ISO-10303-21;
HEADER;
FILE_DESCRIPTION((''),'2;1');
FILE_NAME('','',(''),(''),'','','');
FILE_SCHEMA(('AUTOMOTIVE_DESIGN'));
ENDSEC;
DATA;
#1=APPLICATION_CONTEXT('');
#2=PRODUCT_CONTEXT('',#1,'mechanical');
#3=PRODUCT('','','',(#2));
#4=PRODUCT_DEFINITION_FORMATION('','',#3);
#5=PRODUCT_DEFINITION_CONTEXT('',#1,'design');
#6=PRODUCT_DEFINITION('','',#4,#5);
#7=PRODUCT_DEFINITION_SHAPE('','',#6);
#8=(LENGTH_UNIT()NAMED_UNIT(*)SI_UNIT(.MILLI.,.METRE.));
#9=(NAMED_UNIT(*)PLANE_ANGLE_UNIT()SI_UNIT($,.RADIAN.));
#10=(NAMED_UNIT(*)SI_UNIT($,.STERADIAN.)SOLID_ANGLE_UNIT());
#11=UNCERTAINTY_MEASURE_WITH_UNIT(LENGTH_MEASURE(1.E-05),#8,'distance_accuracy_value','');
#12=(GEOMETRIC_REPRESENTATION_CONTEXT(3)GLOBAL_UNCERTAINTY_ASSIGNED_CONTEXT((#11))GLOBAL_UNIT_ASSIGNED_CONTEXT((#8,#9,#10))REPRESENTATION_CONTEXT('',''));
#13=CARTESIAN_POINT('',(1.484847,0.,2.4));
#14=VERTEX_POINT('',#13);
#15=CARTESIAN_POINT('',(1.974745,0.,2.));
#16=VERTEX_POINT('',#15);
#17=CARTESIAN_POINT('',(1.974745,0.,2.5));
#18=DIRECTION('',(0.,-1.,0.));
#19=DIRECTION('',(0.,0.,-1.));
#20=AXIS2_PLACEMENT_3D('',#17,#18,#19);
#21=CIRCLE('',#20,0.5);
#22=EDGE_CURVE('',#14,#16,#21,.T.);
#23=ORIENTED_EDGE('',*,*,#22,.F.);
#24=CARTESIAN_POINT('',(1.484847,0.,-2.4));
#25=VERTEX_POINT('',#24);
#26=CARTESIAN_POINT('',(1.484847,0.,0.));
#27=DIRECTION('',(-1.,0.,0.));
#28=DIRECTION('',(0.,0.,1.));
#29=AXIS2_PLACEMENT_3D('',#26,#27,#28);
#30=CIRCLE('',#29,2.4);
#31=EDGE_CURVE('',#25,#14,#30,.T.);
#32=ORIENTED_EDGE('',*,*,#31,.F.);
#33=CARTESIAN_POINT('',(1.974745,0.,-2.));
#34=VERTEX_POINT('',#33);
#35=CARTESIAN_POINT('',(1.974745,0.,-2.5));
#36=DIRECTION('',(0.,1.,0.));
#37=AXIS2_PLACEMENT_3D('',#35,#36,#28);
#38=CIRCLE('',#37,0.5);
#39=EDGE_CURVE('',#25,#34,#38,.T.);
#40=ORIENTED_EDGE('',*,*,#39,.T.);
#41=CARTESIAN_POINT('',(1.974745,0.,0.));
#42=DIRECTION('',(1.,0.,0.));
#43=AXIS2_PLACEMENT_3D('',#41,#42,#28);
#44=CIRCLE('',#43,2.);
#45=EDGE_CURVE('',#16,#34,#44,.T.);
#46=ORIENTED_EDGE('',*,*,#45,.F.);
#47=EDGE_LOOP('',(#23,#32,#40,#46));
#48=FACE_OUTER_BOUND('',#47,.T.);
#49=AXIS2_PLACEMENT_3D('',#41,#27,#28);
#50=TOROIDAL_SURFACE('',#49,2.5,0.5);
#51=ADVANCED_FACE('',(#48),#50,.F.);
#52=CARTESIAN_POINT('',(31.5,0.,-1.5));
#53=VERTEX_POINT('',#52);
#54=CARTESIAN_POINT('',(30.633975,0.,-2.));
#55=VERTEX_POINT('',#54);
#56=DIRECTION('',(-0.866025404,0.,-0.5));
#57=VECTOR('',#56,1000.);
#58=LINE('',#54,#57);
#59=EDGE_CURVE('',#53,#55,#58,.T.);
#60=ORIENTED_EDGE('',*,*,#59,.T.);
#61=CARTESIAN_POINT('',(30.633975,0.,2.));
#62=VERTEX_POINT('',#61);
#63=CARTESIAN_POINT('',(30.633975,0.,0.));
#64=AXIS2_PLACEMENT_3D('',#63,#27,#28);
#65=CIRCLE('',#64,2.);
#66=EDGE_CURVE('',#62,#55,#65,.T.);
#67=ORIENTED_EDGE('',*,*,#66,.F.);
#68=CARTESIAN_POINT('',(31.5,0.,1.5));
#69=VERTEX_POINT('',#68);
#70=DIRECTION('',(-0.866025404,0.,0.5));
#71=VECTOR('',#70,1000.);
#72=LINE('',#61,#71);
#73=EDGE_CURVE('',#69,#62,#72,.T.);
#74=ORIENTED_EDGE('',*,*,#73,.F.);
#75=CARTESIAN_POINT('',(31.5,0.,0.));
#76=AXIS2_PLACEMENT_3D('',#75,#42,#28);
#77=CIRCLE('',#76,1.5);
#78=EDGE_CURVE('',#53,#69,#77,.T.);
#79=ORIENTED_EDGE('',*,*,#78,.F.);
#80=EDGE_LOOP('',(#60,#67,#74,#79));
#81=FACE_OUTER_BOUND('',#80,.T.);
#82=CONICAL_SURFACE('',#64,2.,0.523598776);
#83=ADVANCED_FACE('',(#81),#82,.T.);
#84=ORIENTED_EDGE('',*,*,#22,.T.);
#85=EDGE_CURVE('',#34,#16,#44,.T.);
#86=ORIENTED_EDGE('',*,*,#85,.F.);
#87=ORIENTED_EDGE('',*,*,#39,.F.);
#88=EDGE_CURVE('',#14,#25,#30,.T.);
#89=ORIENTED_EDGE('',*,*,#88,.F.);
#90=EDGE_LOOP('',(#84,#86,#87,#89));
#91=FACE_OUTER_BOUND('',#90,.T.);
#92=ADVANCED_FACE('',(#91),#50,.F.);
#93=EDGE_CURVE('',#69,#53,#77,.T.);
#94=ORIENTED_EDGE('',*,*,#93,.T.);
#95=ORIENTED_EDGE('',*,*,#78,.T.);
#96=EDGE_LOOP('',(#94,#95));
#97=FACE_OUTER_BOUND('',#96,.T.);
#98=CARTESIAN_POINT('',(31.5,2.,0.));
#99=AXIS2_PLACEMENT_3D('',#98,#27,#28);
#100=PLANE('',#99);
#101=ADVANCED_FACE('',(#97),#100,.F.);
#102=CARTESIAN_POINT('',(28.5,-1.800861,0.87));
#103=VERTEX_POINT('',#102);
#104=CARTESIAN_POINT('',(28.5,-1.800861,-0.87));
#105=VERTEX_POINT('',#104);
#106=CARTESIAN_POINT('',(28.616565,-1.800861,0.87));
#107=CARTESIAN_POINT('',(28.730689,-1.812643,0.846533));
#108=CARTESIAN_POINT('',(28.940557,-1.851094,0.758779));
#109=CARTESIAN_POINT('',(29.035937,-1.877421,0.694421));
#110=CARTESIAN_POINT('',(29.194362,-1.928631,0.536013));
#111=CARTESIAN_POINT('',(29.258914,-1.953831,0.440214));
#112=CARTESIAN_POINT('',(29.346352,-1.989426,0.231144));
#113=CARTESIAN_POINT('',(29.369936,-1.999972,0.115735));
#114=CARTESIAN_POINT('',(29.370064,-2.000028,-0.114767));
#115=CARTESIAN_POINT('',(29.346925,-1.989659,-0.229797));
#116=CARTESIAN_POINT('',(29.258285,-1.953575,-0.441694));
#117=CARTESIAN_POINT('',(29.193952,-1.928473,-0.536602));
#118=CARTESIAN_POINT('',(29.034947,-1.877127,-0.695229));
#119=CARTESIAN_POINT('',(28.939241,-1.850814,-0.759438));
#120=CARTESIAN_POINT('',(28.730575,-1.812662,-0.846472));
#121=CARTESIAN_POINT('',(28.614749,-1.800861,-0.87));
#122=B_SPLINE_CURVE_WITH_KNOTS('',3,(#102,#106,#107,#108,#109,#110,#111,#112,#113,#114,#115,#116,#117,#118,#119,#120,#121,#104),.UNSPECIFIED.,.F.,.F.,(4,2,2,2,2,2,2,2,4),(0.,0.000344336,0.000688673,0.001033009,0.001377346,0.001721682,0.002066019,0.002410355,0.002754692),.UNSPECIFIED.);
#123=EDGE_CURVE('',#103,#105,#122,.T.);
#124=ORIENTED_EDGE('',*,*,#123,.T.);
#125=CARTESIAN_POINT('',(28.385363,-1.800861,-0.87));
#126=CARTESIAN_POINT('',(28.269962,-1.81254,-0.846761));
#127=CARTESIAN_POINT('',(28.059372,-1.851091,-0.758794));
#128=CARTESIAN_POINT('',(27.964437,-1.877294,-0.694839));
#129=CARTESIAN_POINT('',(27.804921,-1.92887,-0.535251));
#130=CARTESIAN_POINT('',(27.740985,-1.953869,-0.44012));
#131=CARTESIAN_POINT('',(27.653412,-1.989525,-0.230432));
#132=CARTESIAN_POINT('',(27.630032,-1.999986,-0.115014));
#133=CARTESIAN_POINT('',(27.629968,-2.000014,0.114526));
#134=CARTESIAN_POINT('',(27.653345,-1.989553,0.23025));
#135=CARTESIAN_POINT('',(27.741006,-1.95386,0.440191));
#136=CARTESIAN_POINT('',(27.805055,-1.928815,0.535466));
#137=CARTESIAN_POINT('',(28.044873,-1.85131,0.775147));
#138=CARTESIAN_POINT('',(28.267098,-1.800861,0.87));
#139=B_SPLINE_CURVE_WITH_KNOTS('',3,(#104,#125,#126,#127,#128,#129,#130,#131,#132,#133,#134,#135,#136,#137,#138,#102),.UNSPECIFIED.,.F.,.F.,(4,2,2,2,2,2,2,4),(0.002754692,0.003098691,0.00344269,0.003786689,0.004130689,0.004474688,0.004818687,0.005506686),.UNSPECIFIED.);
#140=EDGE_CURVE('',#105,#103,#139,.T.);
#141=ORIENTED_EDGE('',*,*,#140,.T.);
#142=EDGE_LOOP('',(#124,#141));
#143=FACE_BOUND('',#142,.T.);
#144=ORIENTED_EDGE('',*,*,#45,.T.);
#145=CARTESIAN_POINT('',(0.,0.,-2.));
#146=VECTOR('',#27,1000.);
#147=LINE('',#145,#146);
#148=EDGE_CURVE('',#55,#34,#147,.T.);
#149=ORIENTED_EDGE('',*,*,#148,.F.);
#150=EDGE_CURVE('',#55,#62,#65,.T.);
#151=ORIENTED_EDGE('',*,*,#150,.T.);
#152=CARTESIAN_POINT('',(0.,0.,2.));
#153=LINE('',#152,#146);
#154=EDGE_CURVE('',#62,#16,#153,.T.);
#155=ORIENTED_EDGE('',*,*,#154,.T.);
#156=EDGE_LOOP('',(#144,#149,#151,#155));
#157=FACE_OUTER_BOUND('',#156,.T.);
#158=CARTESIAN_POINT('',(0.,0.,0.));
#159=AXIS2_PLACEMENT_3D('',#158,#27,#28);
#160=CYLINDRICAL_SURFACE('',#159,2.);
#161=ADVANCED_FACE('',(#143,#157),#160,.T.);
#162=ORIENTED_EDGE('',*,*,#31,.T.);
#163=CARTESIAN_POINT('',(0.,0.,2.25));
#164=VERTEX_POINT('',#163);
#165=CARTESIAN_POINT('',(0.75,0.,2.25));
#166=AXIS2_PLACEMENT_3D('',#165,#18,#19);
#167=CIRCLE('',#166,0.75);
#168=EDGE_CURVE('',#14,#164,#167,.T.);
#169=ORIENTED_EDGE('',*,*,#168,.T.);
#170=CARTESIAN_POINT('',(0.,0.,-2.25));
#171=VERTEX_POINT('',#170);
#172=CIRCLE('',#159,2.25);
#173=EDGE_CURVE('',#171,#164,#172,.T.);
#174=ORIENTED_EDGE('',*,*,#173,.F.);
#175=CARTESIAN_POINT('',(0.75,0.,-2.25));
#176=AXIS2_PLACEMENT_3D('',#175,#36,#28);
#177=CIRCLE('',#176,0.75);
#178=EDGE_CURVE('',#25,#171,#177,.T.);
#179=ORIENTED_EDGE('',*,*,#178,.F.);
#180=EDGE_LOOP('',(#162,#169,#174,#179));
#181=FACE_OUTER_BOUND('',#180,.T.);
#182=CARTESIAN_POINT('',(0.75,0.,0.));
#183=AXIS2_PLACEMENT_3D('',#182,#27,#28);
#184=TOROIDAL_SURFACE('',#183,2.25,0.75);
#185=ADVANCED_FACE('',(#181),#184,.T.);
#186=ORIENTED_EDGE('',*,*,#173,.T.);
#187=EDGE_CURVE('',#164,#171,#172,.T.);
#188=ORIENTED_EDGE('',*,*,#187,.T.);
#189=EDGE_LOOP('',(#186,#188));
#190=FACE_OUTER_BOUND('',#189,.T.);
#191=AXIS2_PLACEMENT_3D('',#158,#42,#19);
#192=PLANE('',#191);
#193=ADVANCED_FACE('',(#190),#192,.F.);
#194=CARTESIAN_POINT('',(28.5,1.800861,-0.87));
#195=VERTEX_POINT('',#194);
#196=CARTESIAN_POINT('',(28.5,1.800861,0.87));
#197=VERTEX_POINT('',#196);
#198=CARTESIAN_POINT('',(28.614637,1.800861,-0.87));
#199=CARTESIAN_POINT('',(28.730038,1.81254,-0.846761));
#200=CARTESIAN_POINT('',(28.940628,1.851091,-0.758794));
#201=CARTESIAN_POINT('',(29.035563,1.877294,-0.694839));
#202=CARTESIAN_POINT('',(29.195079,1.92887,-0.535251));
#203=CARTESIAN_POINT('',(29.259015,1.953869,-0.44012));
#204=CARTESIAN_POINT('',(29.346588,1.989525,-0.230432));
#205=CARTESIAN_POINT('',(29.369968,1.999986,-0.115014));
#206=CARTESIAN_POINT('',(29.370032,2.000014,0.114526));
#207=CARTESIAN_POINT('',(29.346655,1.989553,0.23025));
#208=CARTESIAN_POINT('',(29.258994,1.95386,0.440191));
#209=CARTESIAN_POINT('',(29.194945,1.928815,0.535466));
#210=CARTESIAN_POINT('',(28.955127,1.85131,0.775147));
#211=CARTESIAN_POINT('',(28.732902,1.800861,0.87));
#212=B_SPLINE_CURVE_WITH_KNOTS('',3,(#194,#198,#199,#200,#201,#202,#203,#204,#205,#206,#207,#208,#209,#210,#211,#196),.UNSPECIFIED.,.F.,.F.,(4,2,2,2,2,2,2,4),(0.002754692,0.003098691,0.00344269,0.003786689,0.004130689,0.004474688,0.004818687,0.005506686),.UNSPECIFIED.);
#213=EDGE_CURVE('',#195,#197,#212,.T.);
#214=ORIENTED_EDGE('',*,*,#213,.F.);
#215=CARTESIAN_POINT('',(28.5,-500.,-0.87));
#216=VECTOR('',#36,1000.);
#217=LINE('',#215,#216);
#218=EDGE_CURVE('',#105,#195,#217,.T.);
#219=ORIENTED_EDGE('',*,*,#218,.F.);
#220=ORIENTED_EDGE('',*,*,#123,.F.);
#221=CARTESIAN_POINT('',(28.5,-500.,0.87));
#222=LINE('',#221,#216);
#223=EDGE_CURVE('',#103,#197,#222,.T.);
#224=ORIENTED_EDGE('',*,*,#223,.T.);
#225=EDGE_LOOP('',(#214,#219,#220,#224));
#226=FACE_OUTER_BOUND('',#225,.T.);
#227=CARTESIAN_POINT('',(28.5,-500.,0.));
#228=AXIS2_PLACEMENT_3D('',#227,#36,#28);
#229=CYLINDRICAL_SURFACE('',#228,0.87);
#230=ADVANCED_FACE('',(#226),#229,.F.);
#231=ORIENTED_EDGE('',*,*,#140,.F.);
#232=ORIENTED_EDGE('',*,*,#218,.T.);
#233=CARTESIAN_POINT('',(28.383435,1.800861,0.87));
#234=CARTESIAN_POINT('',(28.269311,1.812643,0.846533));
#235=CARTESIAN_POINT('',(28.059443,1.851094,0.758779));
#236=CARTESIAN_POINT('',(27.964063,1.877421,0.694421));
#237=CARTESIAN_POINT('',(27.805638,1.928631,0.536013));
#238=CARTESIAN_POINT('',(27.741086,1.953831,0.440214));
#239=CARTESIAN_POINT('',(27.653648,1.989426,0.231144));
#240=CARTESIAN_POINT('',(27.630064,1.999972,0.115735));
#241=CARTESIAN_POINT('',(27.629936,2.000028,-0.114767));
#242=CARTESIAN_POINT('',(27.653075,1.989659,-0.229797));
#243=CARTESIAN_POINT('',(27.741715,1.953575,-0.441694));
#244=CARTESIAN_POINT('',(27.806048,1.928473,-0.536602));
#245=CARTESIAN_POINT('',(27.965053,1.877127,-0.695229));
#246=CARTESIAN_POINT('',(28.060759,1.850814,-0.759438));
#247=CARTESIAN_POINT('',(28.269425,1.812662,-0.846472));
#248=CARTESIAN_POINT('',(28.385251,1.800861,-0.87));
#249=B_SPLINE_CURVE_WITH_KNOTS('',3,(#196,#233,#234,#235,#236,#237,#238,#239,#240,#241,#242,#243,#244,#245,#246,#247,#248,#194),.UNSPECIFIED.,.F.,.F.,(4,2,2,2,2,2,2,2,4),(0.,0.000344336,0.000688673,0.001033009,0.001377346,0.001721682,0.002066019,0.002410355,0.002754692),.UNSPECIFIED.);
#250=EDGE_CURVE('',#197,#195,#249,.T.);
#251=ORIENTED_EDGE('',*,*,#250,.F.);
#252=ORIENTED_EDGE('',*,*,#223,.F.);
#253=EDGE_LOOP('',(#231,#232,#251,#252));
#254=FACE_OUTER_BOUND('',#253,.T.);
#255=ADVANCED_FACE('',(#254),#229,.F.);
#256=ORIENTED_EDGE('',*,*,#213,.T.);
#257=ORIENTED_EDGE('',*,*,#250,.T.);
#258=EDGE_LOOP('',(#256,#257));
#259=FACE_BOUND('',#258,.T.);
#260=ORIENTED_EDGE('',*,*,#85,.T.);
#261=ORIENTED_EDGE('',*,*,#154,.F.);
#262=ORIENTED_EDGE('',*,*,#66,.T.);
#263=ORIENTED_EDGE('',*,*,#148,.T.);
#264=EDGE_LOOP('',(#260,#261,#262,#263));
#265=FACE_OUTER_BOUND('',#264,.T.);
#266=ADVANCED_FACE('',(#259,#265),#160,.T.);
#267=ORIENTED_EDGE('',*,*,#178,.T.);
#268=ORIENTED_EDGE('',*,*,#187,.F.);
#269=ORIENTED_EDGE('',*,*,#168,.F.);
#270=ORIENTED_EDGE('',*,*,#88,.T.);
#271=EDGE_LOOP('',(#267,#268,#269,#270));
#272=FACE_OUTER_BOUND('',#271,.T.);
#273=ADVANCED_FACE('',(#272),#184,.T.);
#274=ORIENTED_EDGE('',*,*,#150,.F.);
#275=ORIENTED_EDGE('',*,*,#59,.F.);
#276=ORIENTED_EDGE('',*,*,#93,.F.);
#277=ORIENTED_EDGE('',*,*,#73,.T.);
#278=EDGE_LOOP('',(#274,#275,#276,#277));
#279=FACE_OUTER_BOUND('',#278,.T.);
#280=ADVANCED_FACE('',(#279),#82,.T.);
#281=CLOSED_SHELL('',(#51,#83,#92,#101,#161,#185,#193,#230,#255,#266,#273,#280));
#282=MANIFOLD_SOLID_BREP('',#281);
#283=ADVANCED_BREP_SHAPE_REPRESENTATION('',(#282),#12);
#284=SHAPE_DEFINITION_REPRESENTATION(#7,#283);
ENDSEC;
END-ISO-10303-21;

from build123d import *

# Parameters (mm, degrees)
FILLET_1_R          = 0.5
CHAMFER_1_SIZE      = 0.866025404
CHAMFER_1_SIZE2     = 0.5
SKETCH_2_R          = 0.87
CUT_EXTRUDE_1_DEPTH = 500


with BuildPart() as part:
    # 草图1 → Revolve 700 (revolve)
    with BuildSketch(Plane.XY, mode=Mode.PRIVATE) as revolve_700_sk:
        with BuildLine():
            Line((0, 0), (31.5, 0))
            Line((31.5, 0), (31.5, 2))
            Line((31.5, 2), (1.5, 2))
            Line((1.5, 2), (1.5, 2.25))
            ThreePointArc((1.5, 2.25), (0.75, 3), (0, 2.25))
            Line((0, 2.25), (0, 0))
        make_face()
    revolve(revolve_700_sk.sketch.rotate(Axis((0, 0, 0), (1, 0, 0)), 90), axis=Axis((0, 0, 0), (1, 0, 0)))

    # 圆角1
    fillet_1_edges = [part.edges().sort_by_distance(p)[0] for p in [
        (1.5, 0, -2),
    ]]
    fillet(fillet_1_edges, radius=FILLET_1_R)

    # 倒角1
    chamfer_1_edges = [part.edges().sort_by_distance(p)[0] for p in [
        (31.5, 0, -2),
    ]]
    chamfer_1_side = [part.faces().sort_by_distance(p)[0] for p in [
        (16.737372436, 0, -2),
    ]]
    chamfer(chamfer_1_edges, length=CHAMFER_1_SIZE, length2=CHAMFER_1_SIZE2, reference=chamfer_1_side[0])

    # 草图2 → 切除-拉伸1 (cut, symmetric)
    with BuildSketch(Plane(origin=(0, 0, 0), x_dir=(1, 0, 0), z_dir=(0, 1, 0))):
        with Locations(Location((28.5, 0, 0), (0, 0, 270))):
            Circle(SKETCH_2_R)
    extrude(amount=CUT_EXTRUDE_1_DEPTH, both=True, mode=Mode.SUBTRACT)


solid = part.part
